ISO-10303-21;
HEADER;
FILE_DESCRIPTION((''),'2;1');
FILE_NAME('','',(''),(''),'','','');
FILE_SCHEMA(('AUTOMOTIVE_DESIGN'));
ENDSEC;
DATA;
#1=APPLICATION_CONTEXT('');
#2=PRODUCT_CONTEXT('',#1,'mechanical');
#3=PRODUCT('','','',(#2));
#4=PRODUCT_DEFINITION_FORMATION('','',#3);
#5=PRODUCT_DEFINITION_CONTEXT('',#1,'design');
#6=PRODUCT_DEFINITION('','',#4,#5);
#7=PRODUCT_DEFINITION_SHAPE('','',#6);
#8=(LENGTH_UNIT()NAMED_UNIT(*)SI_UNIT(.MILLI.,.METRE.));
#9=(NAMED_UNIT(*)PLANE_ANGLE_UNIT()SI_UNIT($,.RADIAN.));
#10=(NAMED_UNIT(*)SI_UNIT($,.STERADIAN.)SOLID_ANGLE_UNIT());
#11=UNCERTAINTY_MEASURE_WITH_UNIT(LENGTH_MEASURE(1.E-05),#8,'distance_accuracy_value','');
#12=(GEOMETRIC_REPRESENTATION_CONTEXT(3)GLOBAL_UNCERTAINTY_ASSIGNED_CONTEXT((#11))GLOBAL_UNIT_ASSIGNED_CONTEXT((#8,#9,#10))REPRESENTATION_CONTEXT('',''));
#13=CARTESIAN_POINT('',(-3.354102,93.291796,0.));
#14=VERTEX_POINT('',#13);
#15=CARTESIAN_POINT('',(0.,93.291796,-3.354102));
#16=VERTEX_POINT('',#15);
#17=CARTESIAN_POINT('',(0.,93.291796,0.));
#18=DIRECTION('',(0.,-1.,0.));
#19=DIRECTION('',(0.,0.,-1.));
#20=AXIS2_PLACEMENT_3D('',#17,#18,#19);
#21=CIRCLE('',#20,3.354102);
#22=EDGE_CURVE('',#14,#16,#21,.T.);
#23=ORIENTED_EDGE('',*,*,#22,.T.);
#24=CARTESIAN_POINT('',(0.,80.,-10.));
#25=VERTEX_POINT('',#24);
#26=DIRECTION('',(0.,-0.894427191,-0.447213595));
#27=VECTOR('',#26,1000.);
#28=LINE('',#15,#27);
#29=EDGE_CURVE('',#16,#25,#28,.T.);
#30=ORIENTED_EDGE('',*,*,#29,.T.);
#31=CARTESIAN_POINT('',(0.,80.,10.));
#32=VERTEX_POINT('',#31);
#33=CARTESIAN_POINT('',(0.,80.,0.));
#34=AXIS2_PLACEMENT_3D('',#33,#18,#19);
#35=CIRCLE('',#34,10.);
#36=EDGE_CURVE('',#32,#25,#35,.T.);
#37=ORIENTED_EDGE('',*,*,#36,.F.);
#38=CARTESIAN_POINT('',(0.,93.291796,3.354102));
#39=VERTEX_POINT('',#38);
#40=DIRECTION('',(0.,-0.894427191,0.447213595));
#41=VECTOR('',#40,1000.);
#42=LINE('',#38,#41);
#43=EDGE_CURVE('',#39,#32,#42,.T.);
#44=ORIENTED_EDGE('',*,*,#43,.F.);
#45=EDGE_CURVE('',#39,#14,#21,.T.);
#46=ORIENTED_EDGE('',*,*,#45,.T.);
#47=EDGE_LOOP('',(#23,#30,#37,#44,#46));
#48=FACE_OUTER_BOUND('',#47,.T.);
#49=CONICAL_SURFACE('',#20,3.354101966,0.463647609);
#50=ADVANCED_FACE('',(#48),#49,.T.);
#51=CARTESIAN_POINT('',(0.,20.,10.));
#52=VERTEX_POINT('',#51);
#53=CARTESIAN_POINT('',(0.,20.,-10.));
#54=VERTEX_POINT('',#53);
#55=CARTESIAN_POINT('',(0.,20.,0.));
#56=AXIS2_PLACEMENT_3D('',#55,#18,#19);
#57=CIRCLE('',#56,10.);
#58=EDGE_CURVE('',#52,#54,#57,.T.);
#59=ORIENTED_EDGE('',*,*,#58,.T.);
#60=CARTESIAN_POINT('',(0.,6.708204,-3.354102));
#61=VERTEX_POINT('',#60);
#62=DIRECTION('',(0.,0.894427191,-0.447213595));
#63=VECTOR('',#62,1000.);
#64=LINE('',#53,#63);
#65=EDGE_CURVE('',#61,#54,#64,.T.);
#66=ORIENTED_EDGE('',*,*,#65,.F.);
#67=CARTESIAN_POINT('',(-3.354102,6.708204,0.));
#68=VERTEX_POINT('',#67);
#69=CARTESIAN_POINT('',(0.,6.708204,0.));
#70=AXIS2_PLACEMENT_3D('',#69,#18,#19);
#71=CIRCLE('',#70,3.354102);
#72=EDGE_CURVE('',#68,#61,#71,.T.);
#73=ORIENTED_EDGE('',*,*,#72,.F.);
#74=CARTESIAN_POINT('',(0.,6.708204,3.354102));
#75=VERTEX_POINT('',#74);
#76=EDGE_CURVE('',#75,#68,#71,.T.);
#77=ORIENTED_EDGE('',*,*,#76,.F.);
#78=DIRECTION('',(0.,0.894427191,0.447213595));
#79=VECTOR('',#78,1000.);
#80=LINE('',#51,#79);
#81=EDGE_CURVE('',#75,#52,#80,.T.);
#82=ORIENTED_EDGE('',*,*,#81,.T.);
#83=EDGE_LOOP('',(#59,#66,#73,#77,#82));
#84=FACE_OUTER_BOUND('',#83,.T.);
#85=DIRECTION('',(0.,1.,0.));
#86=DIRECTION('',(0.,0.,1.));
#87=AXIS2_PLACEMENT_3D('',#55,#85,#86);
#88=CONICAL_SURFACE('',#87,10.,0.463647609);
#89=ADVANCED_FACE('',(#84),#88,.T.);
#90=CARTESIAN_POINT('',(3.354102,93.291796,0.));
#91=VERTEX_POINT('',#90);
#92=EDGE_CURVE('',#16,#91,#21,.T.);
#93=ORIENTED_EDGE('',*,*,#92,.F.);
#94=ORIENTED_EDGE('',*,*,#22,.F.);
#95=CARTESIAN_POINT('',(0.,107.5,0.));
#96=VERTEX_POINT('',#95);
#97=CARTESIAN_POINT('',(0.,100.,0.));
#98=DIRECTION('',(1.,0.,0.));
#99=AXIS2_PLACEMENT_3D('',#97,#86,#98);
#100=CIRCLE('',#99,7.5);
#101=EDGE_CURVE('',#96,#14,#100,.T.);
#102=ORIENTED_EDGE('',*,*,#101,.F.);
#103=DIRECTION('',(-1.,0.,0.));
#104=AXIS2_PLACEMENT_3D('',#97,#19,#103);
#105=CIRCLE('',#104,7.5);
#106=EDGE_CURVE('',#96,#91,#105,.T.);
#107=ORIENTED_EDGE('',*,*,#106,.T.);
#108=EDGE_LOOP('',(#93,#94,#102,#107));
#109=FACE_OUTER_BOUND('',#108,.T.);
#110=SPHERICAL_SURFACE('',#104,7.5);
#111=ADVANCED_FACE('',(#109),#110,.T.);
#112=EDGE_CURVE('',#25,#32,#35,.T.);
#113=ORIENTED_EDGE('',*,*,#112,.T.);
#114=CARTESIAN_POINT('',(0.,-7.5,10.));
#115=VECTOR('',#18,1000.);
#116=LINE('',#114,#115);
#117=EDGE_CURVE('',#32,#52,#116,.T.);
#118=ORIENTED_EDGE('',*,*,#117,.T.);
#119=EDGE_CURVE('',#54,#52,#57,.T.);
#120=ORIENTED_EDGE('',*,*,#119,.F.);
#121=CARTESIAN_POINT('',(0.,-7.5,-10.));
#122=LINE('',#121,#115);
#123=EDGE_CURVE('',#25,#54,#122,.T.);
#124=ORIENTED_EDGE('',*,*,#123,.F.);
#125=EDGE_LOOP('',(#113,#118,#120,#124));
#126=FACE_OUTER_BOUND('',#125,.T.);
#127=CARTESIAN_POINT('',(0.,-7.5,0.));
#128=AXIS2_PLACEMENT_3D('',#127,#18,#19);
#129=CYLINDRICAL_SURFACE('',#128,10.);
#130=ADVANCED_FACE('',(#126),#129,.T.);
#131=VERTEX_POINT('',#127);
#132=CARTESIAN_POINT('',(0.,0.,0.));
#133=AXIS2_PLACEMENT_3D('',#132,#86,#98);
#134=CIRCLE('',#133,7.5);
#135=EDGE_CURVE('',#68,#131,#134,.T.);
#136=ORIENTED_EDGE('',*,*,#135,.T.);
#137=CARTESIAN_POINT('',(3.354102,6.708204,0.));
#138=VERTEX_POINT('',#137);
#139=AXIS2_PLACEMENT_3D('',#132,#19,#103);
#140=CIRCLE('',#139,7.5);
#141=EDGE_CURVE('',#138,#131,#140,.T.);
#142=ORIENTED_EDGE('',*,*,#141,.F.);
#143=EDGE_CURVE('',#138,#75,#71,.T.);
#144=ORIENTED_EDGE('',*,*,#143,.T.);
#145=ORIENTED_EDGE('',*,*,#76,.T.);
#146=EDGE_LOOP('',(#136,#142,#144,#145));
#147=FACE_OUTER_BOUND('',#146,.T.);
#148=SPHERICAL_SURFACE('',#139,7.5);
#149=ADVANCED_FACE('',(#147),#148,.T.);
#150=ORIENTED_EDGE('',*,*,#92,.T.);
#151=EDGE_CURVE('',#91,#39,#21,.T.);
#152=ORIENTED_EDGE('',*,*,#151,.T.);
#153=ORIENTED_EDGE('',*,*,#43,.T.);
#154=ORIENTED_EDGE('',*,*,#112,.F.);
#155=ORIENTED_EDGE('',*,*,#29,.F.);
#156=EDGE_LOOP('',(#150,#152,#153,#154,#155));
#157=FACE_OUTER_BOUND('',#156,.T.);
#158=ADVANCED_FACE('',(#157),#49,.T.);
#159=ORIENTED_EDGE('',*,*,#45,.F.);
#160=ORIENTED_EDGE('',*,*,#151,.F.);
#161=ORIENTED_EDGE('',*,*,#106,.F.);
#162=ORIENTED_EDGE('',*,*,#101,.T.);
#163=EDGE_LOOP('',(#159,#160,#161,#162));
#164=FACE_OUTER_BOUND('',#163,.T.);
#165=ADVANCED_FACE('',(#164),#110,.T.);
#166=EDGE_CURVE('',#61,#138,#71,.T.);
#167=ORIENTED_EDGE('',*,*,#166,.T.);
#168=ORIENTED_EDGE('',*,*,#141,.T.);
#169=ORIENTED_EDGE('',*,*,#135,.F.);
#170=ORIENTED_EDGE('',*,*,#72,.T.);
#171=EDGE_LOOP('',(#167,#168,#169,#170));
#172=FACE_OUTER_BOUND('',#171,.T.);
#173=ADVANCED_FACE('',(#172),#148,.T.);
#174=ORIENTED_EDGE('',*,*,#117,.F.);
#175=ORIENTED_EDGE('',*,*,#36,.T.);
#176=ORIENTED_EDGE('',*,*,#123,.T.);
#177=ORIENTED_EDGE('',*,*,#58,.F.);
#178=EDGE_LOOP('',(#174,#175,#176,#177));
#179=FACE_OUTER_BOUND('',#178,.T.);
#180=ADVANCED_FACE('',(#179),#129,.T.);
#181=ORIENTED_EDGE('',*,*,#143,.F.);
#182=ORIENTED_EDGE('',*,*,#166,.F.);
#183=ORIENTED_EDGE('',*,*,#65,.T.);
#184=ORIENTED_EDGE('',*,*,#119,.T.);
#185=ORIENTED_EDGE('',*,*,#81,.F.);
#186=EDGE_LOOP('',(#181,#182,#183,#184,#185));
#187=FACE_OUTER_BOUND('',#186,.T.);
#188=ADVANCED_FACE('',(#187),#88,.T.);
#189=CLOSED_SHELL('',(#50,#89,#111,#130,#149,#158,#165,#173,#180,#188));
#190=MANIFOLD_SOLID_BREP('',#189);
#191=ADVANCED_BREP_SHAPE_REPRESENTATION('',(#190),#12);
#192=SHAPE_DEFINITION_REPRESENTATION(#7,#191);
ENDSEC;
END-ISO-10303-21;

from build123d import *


with BuildPart() as part:
    # Sketch1 → Revolve1 (revolve)
    with BuildSketch(Plane.XY, mode=Mode.PRIVATE) as revolve1_sk:
        with BuildLine():
            Line((-3.354101966, 93.291796068), (-10, 80))
            Line((-10, 80), (-10, 20))
            Line((-10, 20), (-3.354101966, 6.708203932))
            ThreePointArc((-3.354101966, 6.708203932), (-7.299367421, -1.723146904), (0, -7.5))
            Line((0, -7.5), (0, 107.5))
            ThreePointArc((0, 107.5), (-7.299367421, 101.723146904), (-3.354101966, 93.291796068))
        make_face()
    revolve(revolve1_sk.sketch.rotate(Axis((0, -7.5, 0), (0, 1, 0)), 270), axis=Axis((0, -7.5, 0), (0, 1, 0)))


solid = part.part
